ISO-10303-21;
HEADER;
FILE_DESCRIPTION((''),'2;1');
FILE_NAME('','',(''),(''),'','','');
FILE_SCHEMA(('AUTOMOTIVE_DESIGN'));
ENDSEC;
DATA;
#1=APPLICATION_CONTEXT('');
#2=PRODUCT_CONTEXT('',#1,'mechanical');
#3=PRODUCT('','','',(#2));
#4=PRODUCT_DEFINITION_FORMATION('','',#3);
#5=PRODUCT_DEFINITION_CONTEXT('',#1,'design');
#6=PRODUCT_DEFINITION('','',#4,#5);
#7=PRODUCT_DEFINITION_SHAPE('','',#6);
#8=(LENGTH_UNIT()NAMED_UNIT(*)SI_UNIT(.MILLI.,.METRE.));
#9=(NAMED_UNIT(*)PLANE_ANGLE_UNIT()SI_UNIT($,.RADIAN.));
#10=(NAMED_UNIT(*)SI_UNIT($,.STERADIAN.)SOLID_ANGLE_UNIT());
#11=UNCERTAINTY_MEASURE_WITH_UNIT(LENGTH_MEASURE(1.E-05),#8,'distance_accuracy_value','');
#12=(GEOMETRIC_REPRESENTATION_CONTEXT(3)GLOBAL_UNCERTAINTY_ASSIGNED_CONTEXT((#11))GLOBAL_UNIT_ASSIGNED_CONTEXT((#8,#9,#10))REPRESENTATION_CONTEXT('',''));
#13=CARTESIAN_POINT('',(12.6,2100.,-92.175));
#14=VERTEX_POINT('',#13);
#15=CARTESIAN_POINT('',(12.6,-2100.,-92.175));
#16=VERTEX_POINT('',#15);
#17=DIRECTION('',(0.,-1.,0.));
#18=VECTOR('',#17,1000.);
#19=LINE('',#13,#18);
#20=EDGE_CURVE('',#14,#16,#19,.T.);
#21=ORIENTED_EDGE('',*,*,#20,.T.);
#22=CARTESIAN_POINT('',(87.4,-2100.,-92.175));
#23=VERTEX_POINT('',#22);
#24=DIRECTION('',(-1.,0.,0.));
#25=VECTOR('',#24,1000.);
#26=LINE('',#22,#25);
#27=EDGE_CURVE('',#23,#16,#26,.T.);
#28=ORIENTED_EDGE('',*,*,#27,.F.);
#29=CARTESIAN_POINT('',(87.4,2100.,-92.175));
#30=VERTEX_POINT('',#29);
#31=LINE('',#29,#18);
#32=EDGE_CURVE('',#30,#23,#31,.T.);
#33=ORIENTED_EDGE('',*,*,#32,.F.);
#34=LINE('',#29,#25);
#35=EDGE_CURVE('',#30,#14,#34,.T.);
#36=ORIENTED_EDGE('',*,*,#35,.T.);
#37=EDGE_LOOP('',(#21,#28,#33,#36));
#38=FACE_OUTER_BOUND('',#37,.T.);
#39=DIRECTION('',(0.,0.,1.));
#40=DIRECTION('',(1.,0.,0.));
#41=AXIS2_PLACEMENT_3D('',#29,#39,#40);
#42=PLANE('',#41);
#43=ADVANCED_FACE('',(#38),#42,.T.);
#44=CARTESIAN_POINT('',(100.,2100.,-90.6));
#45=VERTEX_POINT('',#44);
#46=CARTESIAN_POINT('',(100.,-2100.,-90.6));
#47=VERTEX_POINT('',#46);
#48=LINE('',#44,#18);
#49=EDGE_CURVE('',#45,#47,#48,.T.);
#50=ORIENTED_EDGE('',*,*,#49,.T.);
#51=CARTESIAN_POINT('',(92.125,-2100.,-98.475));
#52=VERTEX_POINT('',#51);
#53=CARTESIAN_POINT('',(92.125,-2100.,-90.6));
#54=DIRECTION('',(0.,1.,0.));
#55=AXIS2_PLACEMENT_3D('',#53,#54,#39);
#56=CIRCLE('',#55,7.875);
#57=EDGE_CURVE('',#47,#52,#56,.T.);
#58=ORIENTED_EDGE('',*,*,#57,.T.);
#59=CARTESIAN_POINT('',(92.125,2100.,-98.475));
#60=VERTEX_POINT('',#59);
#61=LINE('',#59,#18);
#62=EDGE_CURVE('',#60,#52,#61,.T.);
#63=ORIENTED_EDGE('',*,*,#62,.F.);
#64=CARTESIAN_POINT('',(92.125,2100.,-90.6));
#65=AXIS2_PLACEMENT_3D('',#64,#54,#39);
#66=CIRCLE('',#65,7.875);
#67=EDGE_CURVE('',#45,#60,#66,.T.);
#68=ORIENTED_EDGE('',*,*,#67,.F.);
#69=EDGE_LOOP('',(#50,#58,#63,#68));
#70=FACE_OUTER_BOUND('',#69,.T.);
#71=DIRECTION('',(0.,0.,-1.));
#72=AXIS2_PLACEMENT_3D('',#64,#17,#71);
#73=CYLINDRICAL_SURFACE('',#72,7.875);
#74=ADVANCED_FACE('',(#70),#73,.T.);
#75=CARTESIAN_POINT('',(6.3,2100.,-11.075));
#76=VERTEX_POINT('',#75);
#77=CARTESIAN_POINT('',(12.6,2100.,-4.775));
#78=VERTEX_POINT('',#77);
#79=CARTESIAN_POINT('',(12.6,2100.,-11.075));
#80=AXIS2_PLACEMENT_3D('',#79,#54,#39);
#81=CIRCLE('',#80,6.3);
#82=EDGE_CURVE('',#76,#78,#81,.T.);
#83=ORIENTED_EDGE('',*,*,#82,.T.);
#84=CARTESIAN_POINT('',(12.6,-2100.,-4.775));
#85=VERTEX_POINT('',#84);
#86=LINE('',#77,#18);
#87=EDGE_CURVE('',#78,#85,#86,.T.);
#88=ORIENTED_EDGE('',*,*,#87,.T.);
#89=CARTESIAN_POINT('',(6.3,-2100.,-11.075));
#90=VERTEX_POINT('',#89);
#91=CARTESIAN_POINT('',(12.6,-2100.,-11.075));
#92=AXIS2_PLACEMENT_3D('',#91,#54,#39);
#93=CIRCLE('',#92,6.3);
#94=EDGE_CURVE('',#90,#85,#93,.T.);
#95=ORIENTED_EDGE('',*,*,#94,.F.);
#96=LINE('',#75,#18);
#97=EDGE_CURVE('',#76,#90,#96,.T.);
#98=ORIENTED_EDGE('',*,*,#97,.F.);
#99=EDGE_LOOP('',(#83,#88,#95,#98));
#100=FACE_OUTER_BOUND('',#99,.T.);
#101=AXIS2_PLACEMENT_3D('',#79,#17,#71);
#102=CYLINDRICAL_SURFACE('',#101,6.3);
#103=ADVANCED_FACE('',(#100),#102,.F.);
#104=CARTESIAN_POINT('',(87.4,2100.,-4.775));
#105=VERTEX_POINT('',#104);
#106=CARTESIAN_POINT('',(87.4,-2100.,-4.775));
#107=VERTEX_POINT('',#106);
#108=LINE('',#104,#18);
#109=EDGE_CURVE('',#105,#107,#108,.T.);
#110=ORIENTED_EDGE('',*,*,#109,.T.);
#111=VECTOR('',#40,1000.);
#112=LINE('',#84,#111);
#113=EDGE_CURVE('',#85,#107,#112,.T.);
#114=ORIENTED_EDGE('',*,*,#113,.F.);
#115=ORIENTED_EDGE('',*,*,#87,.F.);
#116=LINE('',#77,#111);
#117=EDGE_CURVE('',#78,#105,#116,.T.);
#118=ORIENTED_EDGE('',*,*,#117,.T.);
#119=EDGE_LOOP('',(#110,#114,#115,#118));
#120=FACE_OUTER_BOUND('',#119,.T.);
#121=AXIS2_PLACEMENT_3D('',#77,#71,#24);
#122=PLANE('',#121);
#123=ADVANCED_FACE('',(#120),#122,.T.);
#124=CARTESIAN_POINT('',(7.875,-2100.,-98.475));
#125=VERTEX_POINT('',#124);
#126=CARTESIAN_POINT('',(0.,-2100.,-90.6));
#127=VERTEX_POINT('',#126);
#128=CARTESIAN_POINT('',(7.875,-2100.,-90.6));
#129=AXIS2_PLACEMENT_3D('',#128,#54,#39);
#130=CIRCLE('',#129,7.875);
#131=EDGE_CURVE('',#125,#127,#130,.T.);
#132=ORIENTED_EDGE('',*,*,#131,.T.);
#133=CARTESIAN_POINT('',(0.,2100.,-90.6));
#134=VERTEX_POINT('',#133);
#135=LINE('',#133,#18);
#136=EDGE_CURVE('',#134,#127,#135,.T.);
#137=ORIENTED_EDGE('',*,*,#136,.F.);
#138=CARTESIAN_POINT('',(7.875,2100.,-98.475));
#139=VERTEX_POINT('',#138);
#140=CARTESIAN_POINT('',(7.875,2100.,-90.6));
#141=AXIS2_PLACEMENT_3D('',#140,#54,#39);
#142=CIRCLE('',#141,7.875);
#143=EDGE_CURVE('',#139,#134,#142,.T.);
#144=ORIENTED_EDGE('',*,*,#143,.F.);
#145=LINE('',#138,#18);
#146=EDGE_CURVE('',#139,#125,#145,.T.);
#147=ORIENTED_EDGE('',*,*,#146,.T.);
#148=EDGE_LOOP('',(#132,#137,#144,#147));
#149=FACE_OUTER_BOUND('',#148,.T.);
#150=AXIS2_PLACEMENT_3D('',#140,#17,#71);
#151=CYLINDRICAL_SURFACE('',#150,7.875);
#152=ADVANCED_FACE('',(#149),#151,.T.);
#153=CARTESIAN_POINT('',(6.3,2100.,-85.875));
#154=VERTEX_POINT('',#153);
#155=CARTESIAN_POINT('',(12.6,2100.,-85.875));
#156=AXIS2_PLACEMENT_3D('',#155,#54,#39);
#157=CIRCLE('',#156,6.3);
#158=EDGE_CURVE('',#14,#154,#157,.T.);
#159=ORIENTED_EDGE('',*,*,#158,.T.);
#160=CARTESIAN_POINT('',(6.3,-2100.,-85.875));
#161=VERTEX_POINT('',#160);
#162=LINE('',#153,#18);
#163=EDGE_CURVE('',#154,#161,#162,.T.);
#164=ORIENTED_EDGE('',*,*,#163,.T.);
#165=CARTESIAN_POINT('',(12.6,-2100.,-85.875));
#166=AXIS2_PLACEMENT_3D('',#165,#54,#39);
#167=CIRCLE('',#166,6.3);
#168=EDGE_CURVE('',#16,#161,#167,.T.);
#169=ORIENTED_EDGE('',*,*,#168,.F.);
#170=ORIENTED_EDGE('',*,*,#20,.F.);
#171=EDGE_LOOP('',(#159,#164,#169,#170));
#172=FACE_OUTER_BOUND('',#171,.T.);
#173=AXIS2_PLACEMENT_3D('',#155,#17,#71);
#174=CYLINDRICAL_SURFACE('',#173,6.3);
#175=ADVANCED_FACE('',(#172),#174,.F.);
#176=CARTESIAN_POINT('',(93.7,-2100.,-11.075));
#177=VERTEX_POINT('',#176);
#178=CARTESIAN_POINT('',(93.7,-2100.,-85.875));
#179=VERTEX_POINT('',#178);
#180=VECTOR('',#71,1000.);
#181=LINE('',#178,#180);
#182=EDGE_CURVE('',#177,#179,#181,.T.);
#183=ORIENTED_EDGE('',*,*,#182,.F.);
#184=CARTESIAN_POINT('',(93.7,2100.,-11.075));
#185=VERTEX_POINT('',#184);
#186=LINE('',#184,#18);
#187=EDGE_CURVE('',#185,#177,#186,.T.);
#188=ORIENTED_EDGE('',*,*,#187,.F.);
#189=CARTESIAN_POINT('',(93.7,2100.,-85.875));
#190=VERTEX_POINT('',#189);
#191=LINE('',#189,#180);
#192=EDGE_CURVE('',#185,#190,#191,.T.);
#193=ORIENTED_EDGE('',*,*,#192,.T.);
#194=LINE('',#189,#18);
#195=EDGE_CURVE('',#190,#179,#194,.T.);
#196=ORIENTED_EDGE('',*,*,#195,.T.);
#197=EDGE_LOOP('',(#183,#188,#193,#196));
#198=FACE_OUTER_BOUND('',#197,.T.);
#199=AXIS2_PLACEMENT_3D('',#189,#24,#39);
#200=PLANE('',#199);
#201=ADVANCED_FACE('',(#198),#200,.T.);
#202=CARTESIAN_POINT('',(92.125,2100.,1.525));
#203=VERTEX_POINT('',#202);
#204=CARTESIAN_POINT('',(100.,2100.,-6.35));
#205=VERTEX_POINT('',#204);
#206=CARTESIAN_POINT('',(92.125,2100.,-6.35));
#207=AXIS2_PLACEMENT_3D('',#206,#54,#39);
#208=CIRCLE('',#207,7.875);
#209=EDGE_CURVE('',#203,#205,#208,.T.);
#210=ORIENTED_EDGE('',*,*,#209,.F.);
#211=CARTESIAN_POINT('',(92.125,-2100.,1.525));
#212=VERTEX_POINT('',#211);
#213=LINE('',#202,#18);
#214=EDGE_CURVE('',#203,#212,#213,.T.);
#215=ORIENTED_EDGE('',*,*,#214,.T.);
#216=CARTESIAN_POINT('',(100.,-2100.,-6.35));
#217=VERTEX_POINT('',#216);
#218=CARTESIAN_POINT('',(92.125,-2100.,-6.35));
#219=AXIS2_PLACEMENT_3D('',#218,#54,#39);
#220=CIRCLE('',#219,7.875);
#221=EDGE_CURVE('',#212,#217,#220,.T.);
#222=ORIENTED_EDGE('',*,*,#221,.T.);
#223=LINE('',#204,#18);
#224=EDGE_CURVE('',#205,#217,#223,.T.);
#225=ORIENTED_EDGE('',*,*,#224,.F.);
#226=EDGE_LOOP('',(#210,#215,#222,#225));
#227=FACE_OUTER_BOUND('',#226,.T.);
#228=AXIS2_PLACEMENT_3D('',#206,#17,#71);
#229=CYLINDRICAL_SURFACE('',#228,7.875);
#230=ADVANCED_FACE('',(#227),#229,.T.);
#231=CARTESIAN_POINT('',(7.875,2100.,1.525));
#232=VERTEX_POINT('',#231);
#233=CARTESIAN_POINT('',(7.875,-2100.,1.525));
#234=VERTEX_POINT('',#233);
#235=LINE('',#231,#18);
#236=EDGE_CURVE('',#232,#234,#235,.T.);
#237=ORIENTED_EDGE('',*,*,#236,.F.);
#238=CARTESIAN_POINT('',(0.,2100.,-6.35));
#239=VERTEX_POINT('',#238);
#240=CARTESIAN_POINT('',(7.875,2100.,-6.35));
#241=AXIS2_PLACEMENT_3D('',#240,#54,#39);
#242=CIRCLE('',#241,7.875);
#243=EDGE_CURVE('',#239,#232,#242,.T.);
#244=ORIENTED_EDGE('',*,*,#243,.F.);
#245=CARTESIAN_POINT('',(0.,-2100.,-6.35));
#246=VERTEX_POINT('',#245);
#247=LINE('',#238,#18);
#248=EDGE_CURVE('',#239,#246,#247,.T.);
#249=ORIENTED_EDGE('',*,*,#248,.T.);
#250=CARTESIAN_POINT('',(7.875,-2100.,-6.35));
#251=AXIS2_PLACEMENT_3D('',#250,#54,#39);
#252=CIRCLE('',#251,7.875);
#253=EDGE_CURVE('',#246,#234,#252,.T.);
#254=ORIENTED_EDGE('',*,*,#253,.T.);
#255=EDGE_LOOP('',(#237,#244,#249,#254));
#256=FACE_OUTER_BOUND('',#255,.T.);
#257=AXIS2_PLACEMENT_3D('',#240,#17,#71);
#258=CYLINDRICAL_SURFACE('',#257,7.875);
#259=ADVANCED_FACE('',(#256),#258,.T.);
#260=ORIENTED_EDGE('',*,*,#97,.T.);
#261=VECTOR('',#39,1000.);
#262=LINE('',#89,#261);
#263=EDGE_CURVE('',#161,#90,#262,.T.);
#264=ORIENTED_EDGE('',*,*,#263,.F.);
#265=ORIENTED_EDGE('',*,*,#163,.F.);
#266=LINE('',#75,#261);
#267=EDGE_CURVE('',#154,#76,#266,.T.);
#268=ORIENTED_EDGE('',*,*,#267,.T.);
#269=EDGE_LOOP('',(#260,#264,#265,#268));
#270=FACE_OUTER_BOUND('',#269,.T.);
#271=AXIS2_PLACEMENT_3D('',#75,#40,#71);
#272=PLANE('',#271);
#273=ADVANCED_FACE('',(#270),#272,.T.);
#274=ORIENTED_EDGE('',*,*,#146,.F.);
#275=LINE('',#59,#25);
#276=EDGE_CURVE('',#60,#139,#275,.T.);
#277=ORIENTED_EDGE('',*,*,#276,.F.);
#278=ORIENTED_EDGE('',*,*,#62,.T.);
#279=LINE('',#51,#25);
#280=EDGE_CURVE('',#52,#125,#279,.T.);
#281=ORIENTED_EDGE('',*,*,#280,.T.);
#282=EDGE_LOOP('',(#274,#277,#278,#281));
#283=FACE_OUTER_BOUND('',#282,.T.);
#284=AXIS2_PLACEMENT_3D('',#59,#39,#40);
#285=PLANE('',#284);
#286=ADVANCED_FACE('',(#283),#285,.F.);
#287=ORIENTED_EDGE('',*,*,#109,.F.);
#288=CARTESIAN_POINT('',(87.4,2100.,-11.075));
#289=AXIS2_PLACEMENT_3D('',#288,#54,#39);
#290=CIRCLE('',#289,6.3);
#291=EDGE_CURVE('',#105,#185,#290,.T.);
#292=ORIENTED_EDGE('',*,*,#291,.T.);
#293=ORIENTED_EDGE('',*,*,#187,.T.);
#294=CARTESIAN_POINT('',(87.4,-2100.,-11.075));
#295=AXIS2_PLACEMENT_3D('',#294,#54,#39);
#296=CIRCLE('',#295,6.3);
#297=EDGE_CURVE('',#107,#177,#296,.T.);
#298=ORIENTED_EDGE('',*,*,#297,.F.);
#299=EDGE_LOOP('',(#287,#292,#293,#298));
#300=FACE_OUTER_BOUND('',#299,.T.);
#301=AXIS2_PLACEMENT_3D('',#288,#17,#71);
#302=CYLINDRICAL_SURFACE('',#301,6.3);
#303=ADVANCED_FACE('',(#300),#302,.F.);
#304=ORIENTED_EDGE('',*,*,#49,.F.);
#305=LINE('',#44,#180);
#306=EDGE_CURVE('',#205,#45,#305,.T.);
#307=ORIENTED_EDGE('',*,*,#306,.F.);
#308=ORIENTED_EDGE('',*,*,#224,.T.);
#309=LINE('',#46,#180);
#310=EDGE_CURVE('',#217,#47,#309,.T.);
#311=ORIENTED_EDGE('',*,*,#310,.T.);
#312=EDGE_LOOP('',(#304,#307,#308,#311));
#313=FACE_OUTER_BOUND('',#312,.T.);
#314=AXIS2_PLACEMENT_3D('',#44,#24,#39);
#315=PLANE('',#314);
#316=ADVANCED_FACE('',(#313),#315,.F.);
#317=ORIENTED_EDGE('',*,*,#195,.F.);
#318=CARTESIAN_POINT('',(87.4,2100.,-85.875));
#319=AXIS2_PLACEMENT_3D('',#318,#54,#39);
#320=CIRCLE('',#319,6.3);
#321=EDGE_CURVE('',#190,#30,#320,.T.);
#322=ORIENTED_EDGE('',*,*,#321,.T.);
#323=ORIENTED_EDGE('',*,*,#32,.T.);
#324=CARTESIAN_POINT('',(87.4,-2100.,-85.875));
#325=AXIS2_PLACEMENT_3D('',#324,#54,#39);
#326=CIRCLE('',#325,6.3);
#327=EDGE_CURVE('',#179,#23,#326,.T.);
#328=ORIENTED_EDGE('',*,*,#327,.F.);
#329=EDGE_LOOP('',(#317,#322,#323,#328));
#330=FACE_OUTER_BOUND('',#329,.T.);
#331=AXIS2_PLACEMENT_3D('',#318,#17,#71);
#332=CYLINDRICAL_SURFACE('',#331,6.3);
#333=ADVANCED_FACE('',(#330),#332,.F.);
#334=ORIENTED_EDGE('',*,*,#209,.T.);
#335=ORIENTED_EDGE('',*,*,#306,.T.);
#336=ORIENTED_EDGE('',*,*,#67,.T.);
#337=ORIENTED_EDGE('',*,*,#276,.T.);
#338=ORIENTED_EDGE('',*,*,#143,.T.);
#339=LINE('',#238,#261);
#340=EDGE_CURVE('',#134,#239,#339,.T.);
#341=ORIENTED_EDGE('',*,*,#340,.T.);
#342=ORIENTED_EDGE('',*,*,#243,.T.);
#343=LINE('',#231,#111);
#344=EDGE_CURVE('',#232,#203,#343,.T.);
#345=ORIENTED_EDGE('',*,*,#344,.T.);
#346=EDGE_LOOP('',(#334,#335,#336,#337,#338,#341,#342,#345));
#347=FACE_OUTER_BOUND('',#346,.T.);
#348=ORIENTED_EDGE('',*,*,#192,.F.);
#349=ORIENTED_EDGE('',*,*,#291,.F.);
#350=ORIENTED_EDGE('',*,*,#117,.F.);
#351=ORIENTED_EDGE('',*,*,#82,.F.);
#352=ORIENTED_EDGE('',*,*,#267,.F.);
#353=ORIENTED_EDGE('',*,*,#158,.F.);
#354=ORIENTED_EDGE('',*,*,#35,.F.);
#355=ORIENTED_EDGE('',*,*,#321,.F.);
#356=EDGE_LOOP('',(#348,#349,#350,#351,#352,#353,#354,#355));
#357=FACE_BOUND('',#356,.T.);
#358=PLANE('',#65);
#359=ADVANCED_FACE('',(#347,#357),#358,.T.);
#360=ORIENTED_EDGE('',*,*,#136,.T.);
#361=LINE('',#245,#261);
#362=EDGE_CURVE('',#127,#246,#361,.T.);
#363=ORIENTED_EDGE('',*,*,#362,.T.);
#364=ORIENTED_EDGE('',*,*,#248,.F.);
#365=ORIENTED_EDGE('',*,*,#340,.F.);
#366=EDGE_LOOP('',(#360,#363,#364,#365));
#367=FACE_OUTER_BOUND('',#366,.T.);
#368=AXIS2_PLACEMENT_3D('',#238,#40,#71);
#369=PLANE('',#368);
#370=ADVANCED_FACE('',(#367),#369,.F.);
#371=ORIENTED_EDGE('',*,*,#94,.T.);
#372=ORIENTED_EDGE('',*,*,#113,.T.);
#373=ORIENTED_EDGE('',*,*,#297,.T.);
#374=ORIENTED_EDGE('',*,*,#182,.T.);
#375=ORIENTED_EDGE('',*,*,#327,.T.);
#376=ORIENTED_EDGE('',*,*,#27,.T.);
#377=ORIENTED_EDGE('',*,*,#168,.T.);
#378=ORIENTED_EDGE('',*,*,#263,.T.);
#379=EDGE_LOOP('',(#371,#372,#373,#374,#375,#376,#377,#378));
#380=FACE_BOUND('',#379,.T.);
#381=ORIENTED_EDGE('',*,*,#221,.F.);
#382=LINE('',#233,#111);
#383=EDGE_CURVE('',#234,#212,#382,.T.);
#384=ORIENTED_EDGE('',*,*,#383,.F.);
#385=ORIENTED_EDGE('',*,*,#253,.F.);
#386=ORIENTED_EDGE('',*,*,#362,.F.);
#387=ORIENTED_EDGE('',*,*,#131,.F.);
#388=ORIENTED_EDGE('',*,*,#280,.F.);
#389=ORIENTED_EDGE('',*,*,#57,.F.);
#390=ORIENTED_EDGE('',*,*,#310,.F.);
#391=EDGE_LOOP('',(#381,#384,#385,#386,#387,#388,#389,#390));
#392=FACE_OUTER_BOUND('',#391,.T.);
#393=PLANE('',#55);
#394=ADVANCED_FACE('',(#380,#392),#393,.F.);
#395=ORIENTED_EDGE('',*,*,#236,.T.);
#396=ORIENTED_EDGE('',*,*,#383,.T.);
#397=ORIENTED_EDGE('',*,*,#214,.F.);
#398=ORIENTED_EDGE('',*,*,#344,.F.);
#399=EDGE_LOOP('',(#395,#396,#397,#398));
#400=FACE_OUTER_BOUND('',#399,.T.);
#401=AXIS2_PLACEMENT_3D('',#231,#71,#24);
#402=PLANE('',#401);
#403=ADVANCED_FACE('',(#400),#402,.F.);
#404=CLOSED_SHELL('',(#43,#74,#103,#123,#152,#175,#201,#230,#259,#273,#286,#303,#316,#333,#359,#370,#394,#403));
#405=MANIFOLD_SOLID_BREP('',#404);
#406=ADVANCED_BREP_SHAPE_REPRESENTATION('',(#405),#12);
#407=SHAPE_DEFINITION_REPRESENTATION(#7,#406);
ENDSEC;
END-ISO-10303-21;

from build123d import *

# Parameters (mm, degrees)
BOSS_EXTRUDE1_DEPTH = 2100


with BuildPart() as part:
    # Sketch2 → Boss-Extrude1 (new, symmetric)
    with BuildSketch(Plane(origin=(0, 0, 0), x_dir=(1, 0, 0), z_dir=(0, 1, 0))):
        with BuildLine():
            Line((7.875, -1.525), (92.125, -1.525))
            ThreePointArc((92.125, -1.525), (97.693465902, 0.781534098), (100, 6.35))
            Line((100, 6.35), (100, 90.6))
            ThreePointArc((100, 90.6), (97.693465902, 96.168465902), (92.125, 98.475))
            Line((92.125, 98.475), (7.875, 98.475))
            ThreePointArc((7.875, 98.475), (2.306534098, 96.168465902), (0, 90.6))
            Line((0, 90.6), (0, 6.35))
            ThreePointArc((0, 6.35), (2.306534098, 0.781534098), (7.875, -1.525))
        make_face()
        with BuildLine():
            Line((12.6, 4.775), (87.4, 4.775))
            ThreePointArc((87.4, 4.775), (91.854772721, 6.620227279), (93.7, 11.075))
            Line((93.7, 11.075), (93.7, 85.875))
            ThreePointArc((93.7, 85.875), (91.854772721, 90.329772721), (87.4, 92.175))
            Line((87.4, 92.175), (12.6, 92.175))
            ThreePointArc((12.6, 92.175), (8.145227279, 90.329772721), (6.3, 85.875))
            Line((6.3, 85.875), (6.3, 11.075))
            ThreePointArc((6.3, 11.075), (8.145227279, 6.620227279), (12.6, 4.775))
        make_face(mode=Mode.SUBTRACT)
    extrude(amount=BOSS_EXTRUDE1_DEPTH, both=True)


solid = part.part
